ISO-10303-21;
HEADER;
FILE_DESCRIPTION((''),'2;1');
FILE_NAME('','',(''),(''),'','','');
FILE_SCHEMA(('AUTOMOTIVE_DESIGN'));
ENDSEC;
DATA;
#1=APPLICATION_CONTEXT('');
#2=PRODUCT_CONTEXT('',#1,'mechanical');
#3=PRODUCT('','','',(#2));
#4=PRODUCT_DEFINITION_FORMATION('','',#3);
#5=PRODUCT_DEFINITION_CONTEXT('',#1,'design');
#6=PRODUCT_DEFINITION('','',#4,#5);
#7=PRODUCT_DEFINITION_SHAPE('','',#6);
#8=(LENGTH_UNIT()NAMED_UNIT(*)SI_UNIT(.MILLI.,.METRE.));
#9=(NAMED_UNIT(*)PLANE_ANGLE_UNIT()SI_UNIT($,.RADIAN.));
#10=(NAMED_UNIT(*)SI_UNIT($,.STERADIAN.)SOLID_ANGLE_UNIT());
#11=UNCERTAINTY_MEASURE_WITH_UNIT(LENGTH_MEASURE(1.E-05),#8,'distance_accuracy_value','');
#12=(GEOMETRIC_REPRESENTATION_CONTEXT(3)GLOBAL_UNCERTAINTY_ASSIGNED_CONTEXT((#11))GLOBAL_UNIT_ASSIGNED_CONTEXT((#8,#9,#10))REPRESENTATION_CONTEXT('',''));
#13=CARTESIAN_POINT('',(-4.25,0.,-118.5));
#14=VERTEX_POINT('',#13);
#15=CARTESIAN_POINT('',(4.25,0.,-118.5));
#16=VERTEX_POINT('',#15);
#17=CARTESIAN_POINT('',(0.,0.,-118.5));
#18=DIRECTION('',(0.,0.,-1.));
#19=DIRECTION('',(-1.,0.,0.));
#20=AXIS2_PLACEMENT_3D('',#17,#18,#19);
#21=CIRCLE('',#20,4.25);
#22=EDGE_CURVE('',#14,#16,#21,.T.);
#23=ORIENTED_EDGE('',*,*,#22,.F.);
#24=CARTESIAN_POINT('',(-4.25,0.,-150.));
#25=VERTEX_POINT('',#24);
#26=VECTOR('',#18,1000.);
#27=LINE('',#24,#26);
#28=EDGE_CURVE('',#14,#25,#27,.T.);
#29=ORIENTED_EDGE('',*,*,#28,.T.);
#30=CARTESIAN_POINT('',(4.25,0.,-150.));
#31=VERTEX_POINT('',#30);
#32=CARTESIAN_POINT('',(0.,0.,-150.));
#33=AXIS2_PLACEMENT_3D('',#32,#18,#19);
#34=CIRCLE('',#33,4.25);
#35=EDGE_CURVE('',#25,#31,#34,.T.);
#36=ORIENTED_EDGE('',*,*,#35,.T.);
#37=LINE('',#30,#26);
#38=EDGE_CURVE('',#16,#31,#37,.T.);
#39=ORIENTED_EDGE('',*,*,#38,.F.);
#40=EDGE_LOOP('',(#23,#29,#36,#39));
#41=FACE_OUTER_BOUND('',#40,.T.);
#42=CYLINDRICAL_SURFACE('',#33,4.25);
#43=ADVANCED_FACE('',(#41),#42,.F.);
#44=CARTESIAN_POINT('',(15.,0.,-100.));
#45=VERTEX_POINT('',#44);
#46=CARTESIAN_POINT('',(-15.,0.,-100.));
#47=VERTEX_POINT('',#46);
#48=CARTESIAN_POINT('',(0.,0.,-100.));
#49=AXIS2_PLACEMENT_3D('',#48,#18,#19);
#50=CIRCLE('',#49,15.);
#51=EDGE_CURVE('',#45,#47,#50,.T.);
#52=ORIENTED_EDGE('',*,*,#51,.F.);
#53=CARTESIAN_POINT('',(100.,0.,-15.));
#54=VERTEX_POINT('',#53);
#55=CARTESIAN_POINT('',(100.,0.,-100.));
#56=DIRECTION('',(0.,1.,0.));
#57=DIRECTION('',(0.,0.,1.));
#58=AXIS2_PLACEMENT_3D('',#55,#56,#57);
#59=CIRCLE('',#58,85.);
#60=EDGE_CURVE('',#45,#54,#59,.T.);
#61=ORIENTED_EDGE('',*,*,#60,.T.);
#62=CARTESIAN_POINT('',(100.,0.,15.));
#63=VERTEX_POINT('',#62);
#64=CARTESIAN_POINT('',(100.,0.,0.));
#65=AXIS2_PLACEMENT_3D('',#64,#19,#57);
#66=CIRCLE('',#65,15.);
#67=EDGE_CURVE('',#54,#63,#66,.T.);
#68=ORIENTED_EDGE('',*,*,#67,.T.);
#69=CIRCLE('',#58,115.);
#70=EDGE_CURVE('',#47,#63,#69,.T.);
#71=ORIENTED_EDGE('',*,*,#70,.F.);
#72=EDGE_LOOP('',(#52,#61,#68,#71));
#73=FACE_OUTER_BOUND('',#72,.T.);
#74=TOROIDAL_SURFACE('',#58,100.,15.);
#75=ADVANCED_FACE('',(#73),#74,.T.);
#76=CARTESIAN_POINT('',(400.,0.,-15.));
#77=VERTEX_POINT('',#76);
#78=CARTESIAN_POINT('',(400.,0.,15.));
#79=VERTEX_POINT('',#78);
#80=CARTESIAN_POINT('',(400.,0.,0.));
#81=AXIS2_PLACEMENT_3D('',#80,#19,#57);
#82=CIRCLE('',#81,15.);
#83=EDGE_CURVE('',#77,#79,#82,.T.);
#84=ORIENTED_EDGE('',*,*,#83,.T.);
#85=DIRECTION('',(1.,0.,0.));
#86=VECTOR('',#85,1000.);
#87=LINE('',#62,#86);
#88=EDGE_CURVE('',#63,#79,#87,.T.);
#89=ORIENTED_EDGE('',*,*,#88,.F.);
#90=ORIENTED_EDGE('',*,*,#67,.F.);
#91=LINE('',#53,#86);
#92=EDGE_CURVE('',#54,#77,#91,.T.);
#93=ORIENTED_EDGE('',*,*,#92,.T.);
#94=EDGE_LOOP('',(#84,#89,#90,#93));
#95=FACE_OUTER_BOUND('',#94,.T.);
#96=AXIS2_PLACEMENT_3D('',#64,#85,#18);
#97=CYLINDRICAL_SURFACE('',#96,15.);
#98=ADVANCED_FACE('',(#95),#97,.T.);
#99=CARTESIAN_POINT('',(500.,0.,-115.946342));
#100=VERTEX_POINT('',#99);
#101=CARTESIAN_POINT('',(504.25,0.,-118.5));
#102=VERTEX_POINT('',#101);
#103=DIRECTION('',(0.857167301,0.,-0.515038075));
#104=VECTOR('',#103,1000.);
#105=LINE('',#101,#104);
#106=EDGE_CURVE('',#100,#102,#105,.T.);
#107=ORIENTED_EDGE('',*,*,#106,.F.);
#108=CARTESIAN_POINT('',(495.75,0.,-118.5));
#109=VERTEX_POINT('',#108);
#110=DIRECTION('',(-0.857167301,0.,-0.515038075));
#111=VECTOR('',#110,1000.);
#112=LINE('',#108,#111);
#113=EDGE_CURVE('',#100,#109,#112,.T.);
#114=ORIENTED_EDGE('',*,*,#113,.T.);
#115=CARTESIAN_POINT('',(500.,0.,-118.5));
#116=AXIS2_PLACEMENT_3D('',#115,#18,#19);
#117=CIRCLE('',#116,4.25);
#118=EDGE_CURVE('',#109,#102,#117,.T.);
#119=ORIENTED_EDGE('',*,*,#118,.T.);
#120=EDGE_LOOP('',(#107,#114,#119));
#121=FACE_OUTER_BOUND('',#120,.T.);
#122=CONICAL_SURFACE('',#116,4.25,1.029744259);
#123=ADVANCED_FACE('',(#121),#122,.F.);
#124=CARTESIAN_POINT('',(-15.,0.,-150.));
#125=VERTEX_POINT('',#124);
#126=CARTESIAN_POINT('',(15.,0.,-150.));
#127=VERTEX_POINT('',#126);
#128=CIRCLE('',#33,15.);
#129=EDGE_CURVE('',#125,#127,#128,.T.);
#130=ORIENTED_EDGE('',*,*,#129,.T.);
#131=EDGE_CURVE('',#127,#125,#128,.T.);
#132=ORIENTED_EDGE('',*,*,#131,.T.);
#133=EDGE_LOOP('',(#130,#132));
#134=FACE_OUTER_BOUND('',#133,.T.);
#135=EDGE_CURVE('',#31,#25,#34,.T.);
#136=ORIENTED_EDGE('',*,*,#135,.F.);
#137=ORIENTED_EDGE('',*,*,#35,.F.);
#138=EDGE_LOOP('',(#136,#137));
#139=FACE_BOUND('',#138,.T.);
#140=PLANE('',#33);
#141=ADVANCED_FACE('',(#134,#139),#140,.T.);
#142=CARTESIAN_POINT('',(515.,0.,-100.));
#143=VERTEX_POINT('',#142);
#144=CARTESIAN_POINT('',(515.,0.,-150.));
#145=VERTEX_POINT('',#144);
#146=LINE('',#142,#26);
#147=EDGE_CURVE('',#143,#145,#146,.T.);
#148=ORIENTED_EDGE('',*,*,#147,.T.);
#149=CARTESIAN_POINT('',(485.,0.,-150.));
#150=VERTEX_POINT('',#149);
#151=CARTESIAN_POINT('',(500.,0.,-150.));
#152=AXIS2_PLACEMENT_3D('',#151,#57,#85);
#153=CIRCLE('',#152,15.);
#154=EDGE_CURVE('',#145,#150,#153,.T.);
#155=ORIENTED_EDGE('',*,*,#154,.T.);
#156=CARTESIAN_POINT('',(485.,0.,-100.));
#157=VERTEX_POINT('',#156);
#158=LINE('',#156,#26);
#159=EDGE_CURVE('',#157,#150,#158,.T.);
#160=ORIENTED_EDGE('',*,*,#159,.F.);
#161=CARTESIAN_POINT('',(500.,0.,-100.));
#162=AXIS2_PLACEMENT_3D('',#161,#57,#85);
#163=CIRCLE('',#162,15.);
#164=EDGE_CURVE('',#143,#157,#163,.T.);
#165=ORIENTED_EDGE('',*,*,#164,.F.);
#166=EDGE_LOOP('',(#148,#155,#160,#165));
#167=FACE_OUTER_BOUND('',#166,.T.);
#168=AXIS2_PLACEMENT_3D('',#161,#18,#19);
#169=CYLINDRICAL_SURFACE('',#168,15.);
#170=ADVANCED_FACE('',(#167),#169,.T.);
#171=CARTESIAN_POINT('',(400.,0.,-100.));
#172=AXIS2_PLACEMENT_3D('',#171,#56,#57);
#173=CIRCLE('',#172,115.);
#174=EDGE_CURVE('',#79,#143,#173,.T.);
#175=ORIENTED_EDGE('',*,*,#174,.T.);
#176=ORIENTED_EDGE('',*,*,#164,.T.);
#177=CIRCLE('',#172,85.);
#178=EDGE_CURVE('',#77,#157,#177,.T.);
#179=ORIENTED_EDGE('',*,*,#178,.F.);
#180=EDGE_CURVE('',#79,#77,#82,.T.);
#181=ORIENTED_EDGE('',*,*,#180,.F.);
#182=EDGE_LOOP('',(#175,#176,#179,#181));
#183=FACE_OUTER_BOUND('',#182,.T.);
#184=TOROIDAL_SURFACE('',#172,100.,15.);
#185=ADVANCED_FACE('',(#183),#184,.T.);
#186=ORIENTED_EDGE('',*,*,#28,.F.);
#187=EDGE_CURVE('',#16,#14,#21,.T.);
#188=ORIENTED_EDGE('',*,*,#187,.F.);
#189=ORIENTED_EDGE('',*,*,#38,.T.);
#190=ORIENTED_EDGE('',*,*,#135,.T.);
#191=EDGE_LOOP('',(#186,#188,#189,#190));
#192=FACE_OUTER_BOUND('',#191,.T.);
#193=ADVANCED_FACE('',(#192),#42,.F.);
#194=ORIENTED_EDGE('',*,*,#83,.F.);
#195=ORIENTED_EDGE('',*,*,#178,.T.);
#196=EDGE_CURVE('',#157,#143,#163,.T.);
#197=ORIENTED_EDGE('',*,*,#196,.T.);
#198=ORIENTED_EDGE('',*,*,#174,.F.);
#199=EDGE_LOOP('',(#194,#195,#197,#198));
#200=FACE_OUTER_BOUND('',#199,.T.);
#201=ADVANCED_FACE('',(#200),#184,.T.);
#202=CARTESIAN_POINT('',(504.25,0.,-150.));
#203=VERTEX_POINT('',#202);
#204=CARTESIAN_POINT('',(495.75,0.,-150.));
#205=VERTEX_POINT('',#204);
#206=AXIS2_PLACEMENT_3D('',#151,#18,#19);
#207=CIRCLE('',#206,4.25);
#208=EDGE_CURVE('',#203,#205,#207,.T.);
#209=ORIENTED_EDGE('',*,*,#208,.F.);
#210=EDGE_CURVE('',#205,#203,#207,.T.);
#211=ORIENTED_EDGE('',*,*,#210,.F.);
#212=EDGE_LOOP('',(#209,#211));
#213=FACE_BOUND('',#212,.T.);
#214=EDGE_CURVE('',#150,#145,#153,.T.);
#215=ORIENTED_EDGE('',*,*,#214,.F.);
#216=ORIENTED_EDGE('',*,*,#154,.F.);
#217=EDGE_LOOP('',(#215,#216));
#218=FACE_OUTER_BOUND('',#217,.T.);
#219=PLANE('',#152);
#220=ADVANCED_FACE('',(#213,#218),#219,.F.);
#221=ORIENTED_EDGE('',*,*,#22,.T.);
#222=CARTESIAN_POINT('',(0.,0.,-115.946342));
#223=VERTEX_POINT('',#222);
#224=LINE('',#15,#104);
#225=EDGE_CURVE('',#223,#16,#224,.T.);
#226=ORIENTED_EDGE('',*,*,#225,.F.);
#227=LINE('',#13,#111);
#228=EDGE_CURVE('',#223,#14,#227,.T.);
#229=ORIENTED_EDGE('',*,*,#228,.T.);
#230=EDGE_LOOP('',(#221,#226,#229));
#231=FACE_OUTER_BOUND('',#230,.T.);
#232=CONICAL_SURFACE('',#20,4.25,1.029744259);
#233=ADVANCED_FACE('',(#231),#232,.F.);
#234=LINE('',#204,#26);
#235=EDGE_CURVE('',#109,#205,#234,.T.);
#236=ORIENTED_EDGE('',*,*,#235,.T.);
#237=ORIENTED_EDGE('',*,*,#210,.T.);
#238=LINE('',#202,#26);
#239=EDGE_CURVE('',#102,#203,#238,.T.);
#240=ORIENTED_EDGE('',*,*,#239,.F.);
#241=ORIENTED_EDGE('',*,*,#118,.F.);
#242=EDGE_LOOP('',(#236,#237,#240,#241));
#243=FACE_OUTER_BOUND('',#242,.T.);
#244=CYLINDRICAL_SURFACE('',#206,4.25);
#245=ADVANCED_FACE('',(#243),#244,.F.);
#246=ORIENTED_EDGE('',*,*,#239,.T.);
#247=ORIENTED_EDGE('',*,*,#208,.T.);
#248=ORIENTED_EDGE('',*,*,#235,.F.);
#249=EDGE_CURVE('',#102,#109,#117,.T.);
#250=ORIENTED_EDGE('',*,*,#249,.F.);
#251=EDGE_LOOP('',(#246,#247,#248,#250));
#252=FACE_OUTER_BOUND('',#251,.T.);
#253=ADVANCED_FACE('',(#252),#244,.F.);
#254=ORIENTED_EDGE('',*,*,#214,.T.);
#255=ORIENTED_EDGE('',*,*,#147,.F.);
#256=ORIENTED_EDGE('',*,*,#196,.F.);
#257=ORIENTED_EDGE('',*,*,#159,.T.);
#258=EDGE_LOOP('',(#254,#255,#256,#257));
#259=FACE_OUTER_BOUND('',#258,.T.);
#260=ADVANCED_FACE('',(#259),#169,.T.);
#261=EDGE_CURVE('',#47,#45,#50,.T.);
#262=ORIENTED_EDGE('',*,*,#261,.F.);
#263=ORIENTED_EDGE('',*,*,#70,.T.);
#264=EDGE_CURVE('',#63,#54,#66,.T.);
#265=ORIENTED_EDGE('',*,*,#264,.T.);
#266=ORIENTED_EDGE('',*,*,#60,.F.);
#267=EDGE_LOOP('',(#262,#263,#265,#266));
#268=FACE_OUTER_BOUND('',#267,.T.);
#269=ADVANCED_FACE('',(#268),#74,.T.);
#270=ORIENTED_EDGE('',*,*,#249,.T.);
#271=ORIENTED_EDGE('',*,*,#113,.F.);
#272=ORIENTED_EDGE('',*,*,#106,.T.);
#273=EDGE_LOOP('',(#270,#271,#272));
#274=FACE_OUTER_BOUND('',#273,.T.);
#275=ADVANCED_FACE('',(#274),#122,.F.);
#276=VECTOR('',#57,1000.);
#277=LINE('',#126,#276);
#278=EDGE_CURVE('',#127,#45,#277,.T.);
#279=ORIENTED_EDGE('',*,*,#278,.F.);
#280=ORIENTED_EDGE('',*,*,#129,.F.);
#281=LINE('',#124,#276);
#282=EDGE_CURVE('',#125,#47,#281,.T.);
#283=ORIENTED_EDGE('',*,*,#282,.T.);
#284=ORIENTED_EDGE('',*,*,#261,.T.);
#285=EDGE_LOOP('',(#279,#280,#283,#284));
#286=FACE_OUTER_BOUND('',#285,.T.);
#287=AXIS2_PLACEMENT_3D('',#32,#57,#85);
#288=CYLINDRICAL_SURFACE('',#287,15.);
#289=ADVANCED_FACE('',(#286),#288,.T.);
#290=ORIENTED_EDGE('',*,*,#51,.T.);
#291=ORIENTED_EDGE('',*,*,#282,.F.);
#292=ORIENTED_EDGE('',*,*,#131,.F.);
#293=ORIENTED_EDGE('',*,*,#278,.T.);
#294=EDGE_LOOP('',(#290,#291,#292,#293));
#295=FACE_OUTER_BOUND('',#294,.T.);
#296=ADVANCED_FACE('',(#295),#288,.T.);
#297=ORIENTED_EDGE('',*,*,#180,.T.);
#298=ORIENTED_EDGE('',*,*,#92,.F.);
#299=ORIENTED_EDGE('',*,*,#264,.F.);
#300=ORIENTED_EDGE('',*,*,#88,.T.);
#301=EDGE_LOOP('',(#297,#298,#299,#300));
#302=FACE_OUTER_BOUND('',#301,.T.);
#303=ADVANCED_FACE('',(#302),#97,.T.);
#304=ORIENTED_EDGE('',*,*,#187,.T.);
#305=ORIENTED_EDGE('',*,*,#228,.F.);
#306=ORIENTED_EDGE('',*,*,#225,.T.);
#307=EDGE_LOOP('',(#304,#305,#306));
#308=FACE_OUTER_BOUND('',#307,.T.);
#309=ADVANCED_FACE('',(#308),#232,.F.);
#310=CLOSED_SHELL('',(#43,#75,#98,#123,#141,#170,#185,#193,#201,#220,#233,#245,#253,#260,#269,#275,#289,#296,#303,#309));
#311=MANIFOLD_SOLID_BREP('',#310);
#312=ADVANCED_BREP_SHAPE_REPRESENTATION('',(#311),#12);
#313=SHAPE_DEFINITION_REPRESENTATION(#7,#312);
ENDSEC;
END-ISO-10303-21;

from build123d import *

# Parameters (mm, degrees)
SWEEP1_PROFILE_R       = 15
M10_TAPPED_HOLE1_D     = 8.5
M10_TAPPED_HOLE1_DEPTH = 31.5
M10_TAPPED_HOLE1_TIP   = 2.553657631


with BuildPart() as part:
    # Sweep1: sweep along a path in Sketch1
    with BuildLine(Plane(origin=(0, 0, 0), x_dir=(1, 0, 0), z_dir=(0, 1, 0))) as sweep1_path:
        Line((500, 150), (500, 100))
        ThreePointArc((500, 100), (470.710678119, 29.289321881), (400, 0))
        Line((400, 0), (100, 0))
        ThreePointArc((100, 0), (29.289321881, 29.289321881), (0, 100))
        Line((0, 100), (0, 150))
    # Sweep1 profile (on start of the path) → Sweep1 (sweep)
    with BuildSketch(Plane(origin=(500, 0, -150), x_dir=(1, 0, 0), z_dir=(0, 0, 1))):
        Circle(SWEEP1_PROFILE_R)
    sweep(path=sweep1_path.line)

    # M10 Tapped Hole1
    with Locations(Plane(origin=(0, 0, -150), x_dir=(-1, 0, 0), z_dir=(0, 0, -1))):
        with Locations((-500, 0), (0, 0)):
            Hole(M10_TAPPED_HOLE1_D / 2, depth=M10_TAPPED_HOLE1_DEPTH)
            with Locations((0, 0, -(M10_TAPPED_HOLE1_DEPTH + M10_TAPPED_HOLE1_TIP / 2))):  # 118° drill point
                Cone(0, M10_TAPPED_HOLE1_D / 2, M10_TAPPED_HOLE1_TIP, mode=Mode.SUBTRACT)


solid = part.part
